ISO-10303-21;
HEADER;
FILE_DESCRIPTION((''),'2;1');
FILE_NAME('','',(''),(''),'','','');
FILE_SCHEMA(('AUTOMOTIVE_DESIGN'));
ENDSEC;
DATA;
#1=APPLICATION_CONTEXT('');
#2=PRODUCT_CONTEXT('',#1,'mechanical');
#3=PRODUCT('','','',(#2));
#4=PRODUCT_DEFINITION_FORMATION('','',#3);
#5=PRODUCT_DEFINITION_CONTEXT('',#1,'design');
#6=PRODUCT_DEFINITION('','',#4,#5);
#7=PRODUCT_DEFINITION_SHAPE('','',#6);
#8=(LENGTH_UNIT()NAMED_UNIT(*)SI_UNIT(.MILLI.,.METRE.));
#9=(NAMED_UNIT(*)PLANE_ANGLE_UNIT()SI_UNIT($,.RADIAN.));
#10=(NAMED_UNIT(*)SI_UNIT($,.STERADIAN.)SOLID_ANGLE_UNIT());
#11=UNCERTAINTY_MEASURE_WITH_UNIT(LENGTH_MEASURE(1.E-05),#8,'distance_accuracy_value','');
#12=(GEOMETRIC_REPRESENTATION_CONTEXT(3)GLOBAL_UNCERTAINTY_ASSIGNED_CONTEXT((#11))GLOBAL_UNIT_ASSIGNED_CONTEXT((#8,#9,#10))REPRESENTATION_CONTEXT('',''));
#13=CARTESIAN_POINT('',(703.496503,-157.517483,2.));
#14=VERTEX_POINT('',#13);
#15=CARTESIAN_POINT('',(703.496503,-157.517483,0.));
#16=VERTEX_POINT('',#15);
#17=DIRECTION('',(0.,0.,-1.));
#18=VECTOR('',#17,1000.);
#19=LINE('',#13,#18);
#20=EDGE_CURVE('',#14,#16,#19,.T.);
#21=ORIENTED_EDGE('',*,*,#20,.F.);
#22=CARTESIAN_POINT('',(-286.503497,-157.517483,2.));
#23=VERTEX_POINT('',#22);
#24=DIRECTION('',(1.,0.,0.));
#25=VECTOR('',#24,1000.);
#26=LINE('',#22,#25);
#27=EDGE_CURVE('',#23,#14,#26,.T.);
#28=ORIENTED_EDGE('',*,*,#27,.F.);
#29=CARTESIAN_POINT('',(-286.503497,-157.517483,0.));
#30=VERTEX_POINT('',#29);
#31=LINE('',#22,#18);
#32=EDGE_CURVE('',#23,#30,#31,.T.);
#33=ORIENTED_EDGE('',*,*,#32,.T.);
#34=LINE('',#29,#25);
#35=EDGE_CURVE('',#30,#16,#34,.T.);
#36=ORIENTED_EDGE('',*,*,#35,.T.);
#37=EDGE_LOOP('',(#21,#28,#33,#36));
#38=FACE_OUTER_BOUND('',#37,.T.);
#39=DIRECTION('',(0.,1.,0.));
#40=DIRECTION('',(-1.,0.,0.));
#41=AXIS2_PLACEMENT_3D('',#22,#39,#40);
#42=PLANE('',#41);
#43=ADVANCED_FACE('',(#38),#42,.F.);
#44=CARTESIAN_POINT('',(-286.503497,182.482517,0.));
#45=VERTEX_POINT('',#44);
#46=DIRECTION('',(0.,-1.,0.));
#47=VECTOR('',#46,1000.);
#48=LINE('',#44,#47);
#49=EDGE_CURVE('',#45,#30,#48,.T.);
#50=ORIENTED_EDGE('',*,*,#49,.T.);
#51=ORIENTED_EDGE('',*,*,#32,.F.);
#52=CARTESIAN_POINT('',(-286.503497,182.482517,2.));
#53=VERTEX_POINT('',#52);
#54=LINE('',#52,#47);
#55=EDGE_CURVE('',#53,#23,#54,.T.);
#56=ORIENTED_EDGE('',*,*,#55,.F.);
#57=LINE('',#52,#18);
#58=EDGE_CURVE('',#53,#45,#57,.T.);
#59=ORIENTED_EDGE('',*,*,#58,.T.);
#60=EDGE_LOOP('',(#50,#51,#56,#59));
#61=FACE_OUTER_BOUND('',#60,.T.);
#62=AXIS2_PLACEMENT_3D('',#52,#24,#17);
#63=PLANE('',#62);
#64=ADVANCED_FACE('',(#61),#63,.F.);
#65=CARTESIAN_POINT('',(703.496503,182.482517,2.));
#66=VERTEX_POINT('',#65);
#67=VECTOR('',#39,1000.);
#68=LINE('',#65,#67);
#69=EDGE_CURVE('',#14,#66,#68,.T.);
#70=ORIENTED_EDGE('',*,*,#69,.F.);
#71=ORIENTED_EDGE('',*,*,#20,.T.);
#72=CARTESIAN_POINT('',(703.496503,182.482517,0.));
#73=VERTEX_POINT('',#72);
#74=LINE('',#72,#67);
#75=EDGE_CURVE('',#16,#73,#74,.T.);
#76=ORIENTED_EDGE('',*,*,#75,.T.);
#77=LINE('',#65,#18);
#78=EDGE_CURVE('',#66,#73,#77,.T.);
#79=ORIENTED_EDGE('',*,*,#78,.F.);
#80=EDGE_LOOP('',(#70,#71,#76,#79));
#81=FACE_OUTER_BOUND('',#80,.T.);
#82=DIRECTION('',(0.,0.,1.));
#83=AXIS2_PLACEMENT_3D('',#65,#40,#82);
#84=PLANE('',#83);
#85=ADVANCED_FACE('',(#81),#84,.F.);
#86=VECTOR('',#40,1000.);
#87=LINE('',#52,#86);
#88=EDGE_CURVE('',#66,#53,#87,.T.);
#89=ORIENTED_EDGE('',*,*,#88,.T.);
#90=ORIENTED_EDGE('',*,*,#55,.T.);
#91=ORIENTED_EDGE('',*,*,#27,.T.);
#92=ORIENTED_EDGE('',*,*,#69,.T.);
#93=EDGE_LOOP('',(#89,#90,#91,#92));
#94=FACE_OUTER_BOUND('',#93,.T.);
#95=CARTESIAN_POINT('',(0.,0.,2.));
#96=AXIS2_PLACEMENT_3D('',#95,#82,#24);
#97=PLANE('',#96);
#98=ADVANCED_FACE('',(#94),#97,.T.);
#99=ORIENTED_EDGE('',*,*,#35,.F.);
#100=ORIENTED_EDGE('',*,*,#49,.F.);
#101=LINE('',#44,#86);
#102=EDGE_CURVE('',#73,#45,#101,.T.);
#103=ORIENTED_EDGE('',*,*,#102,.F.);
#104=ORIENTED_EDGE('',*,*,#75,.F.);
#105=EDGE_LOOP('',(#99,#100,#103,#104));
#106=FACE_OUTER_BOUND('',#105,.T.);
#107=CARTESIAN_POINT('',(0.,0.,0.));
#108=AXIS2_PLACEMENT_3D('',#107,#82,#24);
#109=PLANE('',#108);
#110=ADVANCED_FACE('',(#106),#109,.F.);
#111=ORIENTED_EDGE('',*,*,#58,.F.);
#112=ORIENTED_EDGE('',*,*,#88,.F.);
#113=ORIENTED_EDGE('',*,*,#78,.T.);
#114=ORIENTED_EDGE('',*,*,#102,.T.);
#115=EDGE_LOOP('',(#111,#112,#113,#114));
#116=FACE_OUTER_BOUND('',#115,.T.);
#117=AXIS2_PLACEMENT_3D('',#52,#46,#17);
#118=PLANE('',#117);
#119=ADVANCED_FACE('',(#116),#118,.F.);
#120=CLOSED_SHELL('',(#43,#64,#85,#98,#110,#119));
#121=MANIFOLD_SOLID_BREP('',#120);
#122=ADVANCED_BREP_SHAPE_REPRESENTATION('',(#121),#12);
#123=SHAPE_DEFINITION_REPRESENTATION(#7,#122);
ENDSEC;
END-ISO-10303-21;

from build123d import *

# Parameters (mm, degrees)
SKETCH_1_W      = 990
SKETCH_1_H      = 340
EXTRUDE_1_DEPTH = 2


with BuildPart() as part:
    # 草图1 → 凸台-拉伸1 (new body)
    with BuildSketch(Plane.XY):
        with Locations((208.496503497, 12.482517483)):
            Rectangle(SKETCH_1_W, SKETCH_1_H)
    extrude(amount=EXTRUDE_1_DEPTH)


solid = part.part
